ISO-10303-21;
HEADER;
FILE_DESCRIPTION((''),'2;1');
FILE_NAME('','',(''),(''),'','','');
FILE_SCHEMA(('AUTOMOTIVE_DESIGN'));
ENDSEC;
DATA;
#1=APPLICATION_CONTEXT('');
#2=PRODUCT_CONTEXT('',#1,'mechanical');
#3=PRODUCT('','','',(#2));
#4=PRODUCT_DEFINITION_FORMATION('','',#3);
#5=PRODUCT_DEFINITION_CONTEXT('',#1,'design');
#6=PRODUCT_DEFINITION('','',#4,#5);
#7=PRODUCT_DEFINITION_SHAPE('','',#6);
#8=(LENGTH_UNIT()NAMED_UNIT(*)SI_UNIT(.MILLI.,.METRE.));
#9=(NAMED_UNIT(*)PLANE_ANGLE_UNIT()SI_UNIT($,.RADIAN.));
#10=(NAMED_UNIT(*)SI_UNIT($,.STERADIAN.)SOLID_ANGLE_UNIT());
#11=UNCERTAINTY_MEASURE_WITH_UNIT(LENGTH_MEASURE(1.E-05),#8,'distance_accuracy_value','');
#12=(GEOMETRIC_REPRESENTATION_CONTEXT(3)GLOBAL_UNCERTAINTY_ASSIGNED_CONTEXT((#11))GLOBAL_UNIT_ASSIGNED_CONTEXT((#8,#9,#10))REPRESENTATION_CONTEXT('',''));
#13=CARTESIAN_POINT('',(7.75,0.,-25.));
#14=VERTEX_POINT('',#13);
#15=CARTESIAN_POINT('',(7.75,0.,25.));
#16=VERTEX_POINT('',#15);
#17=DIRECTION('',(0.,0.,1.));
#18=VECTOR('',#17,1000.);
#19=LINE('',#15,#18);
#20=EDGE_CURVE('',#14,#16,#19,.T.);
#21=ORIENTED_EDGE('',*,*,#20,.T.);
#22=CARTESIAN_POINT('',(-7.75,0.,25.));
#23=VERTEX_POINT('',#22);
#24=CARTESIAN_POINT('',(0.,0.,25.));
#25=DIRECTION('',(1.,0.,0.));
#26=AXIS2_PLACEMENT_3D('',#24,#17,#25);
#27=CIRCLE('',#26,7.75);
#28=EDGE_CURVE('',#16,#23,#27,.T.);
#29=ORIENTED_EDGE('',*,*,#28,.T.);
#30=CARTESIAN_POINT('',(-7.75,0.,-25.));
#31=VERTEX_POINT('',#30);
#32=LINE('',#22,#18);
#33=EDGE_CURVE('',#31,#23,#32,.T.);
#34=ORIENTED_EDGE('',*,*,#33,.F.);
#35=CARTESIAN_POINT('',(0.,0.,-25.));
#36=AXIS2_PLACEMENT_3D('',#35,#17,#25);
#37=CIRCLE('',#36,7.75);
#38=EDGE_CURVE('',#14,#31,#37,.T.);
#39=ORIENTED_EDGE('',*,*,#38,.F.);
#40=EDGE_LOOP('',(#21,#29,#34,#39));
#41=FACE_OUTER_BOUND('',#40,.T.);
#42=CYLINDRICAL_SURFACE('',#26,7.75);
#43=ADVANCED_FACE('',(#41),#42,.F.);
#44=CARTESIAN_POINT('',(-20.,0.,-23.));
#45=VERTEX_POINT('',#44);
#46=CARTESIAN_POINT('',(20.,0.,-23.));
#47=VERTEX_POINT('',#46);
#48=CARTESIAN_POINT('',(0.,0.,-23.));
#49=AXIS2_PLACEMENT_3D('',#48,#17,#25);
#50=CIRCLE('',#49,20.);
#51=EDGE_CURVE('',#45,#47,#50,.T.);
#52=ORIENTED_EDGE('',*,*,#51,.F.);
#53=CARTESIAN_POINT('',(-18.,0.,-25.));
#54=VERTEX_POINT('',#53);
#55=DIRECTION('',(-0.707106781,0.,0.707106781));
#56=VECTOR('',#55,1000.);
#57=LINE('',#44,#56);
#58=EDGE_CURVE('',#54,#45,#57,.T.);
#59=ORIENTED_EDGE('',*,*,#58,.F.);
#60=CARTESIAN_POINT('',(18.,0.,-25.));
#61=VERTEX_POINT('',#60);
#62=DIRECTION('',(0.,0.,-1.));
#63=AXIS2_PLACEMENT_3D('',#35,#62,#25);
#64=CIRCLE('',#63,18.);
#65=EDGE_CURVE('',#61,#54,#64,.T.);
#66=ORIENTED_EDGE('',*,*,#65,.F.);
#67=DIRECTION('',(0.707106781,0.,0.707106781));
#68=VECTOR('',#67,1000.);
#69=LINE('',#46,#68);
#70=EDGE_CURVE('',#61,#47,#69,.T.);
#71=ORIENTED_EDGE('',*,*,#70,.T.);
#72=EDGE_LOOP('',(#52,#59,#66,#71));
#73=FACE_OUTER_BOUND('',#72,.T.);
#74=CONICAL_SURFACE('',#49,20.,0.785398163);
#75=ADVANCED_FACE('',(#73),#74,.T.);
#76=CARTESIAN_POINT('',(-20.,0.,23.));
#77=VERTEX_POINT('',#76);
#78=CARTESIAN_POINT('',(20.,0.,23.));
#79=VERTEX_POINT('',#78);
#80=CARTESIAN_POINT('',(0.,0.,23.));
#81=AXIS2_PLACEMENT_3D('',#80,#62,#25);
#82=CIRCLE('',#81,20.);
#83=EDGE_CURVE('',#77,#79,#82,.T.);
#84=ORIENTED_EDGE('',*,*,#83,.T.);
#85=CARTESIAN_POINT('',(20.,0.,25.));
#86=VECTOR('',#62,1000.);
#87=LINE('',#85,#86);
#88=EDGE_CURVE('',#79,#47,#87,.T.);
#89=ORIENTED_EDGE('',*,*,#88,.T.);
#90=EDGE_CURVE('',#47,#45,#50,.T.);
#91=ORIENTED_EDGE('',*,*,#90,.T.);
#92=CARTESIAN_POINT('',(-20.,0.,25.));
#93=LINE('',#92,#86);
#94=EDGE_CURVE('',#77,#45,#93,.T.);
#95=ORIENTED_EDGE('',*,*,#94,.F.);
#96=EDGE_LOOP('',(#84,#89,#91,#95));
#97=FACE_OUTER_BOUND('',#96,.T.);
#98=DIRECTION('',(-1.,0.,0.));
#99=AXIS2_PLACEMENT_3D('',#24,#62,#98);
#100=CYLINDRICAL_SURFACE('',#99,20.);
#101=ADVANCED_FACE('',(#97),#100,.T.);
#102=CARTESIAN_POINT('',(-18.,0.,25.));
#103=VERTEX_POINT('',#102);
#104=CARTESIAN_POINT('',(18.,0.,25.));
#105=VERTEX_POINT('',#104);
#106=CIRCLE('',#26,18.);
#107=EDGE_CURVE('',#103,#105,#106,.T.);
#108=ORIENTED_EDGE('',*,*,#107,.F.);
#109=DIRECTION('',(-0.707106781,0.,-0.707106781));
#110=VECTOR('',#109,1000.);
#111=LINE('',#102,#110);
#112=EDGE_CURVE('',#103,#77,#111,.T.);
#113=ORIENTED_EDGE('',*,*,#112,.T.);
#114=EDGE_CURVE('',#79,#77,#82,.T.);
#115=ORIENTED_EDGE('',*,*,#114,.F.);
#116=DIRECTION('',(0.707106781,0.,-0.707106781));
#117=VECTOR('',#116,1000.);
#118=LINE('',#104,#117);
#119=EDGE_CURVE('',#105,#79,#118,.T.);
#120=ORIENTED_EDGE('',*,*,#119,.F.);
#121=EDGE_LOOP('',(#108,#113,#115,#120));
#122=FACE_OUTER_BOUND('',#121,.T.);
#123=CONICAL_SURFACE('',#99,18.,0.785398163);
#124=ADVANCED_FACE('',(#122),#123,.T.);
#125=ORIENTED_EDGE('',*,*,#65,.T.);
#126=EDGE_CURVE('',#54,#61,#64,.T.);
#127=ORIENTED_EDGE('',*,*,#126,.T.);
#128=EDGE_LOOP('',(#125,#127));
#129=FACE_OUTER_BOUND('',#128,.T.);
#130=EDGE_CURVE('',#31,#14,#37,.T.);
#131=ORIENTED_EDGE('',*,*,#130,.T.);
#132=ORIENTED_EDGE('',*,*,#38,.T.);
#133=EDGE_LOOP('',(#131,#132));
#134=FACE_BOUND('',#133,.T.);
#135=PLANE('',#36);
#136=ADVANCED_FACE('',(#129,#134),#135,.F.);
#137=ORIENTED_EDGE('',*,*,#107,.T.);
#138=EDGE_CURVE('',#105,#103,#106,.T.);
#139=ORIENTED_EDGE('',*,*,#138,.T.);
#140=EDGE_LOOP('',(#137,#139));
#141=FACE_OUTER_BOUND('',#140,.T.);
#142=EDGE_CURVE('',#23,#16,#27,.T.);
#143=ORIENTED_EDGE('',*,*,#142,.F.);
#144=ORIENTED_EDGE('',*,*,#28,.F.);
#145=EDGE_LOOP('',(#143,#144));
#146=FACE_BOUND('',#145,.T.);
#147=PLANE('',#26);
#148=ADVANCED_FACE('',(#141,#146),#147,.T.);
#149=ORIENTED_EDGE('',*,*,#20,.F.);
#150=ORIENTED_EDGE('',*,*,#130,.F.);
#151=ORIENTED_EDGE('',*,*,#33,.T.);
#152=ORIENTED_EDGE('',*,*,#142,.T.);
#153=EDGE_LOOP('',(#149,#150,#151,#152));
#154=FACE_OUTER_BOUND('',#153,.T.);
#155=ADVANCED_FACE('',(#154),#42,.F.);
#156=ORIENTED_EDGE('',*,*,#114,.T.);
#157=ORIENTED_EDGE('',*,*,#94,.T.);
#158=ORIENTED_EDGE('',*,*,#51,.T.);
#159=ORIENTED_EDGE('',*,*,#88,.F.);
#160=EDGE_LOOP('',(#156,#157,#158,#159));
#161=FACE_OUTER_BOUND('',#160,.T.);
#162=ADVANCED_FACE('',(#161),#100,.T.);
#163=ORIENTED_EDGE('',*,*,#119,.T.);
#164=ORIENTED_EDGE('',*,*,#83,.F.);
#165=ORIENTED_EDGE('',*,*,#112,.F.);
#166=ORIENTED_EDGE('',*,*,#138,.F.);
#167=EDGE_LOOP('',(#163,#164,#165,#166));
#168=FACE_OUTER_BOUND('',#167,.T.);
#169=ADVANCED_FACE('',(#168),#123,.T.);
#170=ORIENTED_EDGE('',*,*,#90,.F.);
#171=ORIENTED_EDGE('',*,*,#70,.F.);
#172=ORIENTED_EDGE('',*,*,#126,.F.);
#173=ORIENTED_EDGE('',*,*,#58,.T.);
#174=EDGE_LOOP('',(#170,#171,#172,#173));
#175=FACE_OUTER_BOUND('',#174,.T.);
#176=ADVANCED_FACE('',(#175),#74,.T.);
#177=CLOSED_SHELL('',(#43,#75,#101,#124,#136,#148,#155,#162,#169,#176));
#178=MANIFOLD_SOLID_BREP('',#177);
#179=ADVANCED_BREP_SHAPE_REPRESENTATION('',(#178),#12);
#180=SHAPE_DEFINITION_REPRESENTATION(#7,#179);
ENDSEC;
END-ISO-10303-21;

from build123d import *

# Parameters (mm, degrees)
SKETCH1_R           = 20
BOSS_EXTRUDE1_DEPTH = 25
CHAMFER1_SIZE       = 2
M18_TAPPED_HOLE1_D  = 15.5


with BuildPart() as part:
    # Sketch1 → Boss-Extrude1 (new, symmetric)
    with BuildSketch(Plane.XY):
        Circle(SKETCH1_R)
    extrude(amount=BOSS_EXTRUDE1_DEPTH, both=True)

    # Chamfer1
    chamfer1_edges = [part.edges().sort_by_distance(p)[0] for p in [
        (-20, 0, -25),
        (-20, 0, 25),
    ]]
    chamfer(chamfer1_edges, length=CHAMFER1_SIZE)

    # M18 Tapped Hole1 (through all)
    with Locations(Plane.XY.offset(25)):
        with Locations((0, 0)):
            Hole(M18_TAPPED_HOLE1_D / 2)


solid = part.part
